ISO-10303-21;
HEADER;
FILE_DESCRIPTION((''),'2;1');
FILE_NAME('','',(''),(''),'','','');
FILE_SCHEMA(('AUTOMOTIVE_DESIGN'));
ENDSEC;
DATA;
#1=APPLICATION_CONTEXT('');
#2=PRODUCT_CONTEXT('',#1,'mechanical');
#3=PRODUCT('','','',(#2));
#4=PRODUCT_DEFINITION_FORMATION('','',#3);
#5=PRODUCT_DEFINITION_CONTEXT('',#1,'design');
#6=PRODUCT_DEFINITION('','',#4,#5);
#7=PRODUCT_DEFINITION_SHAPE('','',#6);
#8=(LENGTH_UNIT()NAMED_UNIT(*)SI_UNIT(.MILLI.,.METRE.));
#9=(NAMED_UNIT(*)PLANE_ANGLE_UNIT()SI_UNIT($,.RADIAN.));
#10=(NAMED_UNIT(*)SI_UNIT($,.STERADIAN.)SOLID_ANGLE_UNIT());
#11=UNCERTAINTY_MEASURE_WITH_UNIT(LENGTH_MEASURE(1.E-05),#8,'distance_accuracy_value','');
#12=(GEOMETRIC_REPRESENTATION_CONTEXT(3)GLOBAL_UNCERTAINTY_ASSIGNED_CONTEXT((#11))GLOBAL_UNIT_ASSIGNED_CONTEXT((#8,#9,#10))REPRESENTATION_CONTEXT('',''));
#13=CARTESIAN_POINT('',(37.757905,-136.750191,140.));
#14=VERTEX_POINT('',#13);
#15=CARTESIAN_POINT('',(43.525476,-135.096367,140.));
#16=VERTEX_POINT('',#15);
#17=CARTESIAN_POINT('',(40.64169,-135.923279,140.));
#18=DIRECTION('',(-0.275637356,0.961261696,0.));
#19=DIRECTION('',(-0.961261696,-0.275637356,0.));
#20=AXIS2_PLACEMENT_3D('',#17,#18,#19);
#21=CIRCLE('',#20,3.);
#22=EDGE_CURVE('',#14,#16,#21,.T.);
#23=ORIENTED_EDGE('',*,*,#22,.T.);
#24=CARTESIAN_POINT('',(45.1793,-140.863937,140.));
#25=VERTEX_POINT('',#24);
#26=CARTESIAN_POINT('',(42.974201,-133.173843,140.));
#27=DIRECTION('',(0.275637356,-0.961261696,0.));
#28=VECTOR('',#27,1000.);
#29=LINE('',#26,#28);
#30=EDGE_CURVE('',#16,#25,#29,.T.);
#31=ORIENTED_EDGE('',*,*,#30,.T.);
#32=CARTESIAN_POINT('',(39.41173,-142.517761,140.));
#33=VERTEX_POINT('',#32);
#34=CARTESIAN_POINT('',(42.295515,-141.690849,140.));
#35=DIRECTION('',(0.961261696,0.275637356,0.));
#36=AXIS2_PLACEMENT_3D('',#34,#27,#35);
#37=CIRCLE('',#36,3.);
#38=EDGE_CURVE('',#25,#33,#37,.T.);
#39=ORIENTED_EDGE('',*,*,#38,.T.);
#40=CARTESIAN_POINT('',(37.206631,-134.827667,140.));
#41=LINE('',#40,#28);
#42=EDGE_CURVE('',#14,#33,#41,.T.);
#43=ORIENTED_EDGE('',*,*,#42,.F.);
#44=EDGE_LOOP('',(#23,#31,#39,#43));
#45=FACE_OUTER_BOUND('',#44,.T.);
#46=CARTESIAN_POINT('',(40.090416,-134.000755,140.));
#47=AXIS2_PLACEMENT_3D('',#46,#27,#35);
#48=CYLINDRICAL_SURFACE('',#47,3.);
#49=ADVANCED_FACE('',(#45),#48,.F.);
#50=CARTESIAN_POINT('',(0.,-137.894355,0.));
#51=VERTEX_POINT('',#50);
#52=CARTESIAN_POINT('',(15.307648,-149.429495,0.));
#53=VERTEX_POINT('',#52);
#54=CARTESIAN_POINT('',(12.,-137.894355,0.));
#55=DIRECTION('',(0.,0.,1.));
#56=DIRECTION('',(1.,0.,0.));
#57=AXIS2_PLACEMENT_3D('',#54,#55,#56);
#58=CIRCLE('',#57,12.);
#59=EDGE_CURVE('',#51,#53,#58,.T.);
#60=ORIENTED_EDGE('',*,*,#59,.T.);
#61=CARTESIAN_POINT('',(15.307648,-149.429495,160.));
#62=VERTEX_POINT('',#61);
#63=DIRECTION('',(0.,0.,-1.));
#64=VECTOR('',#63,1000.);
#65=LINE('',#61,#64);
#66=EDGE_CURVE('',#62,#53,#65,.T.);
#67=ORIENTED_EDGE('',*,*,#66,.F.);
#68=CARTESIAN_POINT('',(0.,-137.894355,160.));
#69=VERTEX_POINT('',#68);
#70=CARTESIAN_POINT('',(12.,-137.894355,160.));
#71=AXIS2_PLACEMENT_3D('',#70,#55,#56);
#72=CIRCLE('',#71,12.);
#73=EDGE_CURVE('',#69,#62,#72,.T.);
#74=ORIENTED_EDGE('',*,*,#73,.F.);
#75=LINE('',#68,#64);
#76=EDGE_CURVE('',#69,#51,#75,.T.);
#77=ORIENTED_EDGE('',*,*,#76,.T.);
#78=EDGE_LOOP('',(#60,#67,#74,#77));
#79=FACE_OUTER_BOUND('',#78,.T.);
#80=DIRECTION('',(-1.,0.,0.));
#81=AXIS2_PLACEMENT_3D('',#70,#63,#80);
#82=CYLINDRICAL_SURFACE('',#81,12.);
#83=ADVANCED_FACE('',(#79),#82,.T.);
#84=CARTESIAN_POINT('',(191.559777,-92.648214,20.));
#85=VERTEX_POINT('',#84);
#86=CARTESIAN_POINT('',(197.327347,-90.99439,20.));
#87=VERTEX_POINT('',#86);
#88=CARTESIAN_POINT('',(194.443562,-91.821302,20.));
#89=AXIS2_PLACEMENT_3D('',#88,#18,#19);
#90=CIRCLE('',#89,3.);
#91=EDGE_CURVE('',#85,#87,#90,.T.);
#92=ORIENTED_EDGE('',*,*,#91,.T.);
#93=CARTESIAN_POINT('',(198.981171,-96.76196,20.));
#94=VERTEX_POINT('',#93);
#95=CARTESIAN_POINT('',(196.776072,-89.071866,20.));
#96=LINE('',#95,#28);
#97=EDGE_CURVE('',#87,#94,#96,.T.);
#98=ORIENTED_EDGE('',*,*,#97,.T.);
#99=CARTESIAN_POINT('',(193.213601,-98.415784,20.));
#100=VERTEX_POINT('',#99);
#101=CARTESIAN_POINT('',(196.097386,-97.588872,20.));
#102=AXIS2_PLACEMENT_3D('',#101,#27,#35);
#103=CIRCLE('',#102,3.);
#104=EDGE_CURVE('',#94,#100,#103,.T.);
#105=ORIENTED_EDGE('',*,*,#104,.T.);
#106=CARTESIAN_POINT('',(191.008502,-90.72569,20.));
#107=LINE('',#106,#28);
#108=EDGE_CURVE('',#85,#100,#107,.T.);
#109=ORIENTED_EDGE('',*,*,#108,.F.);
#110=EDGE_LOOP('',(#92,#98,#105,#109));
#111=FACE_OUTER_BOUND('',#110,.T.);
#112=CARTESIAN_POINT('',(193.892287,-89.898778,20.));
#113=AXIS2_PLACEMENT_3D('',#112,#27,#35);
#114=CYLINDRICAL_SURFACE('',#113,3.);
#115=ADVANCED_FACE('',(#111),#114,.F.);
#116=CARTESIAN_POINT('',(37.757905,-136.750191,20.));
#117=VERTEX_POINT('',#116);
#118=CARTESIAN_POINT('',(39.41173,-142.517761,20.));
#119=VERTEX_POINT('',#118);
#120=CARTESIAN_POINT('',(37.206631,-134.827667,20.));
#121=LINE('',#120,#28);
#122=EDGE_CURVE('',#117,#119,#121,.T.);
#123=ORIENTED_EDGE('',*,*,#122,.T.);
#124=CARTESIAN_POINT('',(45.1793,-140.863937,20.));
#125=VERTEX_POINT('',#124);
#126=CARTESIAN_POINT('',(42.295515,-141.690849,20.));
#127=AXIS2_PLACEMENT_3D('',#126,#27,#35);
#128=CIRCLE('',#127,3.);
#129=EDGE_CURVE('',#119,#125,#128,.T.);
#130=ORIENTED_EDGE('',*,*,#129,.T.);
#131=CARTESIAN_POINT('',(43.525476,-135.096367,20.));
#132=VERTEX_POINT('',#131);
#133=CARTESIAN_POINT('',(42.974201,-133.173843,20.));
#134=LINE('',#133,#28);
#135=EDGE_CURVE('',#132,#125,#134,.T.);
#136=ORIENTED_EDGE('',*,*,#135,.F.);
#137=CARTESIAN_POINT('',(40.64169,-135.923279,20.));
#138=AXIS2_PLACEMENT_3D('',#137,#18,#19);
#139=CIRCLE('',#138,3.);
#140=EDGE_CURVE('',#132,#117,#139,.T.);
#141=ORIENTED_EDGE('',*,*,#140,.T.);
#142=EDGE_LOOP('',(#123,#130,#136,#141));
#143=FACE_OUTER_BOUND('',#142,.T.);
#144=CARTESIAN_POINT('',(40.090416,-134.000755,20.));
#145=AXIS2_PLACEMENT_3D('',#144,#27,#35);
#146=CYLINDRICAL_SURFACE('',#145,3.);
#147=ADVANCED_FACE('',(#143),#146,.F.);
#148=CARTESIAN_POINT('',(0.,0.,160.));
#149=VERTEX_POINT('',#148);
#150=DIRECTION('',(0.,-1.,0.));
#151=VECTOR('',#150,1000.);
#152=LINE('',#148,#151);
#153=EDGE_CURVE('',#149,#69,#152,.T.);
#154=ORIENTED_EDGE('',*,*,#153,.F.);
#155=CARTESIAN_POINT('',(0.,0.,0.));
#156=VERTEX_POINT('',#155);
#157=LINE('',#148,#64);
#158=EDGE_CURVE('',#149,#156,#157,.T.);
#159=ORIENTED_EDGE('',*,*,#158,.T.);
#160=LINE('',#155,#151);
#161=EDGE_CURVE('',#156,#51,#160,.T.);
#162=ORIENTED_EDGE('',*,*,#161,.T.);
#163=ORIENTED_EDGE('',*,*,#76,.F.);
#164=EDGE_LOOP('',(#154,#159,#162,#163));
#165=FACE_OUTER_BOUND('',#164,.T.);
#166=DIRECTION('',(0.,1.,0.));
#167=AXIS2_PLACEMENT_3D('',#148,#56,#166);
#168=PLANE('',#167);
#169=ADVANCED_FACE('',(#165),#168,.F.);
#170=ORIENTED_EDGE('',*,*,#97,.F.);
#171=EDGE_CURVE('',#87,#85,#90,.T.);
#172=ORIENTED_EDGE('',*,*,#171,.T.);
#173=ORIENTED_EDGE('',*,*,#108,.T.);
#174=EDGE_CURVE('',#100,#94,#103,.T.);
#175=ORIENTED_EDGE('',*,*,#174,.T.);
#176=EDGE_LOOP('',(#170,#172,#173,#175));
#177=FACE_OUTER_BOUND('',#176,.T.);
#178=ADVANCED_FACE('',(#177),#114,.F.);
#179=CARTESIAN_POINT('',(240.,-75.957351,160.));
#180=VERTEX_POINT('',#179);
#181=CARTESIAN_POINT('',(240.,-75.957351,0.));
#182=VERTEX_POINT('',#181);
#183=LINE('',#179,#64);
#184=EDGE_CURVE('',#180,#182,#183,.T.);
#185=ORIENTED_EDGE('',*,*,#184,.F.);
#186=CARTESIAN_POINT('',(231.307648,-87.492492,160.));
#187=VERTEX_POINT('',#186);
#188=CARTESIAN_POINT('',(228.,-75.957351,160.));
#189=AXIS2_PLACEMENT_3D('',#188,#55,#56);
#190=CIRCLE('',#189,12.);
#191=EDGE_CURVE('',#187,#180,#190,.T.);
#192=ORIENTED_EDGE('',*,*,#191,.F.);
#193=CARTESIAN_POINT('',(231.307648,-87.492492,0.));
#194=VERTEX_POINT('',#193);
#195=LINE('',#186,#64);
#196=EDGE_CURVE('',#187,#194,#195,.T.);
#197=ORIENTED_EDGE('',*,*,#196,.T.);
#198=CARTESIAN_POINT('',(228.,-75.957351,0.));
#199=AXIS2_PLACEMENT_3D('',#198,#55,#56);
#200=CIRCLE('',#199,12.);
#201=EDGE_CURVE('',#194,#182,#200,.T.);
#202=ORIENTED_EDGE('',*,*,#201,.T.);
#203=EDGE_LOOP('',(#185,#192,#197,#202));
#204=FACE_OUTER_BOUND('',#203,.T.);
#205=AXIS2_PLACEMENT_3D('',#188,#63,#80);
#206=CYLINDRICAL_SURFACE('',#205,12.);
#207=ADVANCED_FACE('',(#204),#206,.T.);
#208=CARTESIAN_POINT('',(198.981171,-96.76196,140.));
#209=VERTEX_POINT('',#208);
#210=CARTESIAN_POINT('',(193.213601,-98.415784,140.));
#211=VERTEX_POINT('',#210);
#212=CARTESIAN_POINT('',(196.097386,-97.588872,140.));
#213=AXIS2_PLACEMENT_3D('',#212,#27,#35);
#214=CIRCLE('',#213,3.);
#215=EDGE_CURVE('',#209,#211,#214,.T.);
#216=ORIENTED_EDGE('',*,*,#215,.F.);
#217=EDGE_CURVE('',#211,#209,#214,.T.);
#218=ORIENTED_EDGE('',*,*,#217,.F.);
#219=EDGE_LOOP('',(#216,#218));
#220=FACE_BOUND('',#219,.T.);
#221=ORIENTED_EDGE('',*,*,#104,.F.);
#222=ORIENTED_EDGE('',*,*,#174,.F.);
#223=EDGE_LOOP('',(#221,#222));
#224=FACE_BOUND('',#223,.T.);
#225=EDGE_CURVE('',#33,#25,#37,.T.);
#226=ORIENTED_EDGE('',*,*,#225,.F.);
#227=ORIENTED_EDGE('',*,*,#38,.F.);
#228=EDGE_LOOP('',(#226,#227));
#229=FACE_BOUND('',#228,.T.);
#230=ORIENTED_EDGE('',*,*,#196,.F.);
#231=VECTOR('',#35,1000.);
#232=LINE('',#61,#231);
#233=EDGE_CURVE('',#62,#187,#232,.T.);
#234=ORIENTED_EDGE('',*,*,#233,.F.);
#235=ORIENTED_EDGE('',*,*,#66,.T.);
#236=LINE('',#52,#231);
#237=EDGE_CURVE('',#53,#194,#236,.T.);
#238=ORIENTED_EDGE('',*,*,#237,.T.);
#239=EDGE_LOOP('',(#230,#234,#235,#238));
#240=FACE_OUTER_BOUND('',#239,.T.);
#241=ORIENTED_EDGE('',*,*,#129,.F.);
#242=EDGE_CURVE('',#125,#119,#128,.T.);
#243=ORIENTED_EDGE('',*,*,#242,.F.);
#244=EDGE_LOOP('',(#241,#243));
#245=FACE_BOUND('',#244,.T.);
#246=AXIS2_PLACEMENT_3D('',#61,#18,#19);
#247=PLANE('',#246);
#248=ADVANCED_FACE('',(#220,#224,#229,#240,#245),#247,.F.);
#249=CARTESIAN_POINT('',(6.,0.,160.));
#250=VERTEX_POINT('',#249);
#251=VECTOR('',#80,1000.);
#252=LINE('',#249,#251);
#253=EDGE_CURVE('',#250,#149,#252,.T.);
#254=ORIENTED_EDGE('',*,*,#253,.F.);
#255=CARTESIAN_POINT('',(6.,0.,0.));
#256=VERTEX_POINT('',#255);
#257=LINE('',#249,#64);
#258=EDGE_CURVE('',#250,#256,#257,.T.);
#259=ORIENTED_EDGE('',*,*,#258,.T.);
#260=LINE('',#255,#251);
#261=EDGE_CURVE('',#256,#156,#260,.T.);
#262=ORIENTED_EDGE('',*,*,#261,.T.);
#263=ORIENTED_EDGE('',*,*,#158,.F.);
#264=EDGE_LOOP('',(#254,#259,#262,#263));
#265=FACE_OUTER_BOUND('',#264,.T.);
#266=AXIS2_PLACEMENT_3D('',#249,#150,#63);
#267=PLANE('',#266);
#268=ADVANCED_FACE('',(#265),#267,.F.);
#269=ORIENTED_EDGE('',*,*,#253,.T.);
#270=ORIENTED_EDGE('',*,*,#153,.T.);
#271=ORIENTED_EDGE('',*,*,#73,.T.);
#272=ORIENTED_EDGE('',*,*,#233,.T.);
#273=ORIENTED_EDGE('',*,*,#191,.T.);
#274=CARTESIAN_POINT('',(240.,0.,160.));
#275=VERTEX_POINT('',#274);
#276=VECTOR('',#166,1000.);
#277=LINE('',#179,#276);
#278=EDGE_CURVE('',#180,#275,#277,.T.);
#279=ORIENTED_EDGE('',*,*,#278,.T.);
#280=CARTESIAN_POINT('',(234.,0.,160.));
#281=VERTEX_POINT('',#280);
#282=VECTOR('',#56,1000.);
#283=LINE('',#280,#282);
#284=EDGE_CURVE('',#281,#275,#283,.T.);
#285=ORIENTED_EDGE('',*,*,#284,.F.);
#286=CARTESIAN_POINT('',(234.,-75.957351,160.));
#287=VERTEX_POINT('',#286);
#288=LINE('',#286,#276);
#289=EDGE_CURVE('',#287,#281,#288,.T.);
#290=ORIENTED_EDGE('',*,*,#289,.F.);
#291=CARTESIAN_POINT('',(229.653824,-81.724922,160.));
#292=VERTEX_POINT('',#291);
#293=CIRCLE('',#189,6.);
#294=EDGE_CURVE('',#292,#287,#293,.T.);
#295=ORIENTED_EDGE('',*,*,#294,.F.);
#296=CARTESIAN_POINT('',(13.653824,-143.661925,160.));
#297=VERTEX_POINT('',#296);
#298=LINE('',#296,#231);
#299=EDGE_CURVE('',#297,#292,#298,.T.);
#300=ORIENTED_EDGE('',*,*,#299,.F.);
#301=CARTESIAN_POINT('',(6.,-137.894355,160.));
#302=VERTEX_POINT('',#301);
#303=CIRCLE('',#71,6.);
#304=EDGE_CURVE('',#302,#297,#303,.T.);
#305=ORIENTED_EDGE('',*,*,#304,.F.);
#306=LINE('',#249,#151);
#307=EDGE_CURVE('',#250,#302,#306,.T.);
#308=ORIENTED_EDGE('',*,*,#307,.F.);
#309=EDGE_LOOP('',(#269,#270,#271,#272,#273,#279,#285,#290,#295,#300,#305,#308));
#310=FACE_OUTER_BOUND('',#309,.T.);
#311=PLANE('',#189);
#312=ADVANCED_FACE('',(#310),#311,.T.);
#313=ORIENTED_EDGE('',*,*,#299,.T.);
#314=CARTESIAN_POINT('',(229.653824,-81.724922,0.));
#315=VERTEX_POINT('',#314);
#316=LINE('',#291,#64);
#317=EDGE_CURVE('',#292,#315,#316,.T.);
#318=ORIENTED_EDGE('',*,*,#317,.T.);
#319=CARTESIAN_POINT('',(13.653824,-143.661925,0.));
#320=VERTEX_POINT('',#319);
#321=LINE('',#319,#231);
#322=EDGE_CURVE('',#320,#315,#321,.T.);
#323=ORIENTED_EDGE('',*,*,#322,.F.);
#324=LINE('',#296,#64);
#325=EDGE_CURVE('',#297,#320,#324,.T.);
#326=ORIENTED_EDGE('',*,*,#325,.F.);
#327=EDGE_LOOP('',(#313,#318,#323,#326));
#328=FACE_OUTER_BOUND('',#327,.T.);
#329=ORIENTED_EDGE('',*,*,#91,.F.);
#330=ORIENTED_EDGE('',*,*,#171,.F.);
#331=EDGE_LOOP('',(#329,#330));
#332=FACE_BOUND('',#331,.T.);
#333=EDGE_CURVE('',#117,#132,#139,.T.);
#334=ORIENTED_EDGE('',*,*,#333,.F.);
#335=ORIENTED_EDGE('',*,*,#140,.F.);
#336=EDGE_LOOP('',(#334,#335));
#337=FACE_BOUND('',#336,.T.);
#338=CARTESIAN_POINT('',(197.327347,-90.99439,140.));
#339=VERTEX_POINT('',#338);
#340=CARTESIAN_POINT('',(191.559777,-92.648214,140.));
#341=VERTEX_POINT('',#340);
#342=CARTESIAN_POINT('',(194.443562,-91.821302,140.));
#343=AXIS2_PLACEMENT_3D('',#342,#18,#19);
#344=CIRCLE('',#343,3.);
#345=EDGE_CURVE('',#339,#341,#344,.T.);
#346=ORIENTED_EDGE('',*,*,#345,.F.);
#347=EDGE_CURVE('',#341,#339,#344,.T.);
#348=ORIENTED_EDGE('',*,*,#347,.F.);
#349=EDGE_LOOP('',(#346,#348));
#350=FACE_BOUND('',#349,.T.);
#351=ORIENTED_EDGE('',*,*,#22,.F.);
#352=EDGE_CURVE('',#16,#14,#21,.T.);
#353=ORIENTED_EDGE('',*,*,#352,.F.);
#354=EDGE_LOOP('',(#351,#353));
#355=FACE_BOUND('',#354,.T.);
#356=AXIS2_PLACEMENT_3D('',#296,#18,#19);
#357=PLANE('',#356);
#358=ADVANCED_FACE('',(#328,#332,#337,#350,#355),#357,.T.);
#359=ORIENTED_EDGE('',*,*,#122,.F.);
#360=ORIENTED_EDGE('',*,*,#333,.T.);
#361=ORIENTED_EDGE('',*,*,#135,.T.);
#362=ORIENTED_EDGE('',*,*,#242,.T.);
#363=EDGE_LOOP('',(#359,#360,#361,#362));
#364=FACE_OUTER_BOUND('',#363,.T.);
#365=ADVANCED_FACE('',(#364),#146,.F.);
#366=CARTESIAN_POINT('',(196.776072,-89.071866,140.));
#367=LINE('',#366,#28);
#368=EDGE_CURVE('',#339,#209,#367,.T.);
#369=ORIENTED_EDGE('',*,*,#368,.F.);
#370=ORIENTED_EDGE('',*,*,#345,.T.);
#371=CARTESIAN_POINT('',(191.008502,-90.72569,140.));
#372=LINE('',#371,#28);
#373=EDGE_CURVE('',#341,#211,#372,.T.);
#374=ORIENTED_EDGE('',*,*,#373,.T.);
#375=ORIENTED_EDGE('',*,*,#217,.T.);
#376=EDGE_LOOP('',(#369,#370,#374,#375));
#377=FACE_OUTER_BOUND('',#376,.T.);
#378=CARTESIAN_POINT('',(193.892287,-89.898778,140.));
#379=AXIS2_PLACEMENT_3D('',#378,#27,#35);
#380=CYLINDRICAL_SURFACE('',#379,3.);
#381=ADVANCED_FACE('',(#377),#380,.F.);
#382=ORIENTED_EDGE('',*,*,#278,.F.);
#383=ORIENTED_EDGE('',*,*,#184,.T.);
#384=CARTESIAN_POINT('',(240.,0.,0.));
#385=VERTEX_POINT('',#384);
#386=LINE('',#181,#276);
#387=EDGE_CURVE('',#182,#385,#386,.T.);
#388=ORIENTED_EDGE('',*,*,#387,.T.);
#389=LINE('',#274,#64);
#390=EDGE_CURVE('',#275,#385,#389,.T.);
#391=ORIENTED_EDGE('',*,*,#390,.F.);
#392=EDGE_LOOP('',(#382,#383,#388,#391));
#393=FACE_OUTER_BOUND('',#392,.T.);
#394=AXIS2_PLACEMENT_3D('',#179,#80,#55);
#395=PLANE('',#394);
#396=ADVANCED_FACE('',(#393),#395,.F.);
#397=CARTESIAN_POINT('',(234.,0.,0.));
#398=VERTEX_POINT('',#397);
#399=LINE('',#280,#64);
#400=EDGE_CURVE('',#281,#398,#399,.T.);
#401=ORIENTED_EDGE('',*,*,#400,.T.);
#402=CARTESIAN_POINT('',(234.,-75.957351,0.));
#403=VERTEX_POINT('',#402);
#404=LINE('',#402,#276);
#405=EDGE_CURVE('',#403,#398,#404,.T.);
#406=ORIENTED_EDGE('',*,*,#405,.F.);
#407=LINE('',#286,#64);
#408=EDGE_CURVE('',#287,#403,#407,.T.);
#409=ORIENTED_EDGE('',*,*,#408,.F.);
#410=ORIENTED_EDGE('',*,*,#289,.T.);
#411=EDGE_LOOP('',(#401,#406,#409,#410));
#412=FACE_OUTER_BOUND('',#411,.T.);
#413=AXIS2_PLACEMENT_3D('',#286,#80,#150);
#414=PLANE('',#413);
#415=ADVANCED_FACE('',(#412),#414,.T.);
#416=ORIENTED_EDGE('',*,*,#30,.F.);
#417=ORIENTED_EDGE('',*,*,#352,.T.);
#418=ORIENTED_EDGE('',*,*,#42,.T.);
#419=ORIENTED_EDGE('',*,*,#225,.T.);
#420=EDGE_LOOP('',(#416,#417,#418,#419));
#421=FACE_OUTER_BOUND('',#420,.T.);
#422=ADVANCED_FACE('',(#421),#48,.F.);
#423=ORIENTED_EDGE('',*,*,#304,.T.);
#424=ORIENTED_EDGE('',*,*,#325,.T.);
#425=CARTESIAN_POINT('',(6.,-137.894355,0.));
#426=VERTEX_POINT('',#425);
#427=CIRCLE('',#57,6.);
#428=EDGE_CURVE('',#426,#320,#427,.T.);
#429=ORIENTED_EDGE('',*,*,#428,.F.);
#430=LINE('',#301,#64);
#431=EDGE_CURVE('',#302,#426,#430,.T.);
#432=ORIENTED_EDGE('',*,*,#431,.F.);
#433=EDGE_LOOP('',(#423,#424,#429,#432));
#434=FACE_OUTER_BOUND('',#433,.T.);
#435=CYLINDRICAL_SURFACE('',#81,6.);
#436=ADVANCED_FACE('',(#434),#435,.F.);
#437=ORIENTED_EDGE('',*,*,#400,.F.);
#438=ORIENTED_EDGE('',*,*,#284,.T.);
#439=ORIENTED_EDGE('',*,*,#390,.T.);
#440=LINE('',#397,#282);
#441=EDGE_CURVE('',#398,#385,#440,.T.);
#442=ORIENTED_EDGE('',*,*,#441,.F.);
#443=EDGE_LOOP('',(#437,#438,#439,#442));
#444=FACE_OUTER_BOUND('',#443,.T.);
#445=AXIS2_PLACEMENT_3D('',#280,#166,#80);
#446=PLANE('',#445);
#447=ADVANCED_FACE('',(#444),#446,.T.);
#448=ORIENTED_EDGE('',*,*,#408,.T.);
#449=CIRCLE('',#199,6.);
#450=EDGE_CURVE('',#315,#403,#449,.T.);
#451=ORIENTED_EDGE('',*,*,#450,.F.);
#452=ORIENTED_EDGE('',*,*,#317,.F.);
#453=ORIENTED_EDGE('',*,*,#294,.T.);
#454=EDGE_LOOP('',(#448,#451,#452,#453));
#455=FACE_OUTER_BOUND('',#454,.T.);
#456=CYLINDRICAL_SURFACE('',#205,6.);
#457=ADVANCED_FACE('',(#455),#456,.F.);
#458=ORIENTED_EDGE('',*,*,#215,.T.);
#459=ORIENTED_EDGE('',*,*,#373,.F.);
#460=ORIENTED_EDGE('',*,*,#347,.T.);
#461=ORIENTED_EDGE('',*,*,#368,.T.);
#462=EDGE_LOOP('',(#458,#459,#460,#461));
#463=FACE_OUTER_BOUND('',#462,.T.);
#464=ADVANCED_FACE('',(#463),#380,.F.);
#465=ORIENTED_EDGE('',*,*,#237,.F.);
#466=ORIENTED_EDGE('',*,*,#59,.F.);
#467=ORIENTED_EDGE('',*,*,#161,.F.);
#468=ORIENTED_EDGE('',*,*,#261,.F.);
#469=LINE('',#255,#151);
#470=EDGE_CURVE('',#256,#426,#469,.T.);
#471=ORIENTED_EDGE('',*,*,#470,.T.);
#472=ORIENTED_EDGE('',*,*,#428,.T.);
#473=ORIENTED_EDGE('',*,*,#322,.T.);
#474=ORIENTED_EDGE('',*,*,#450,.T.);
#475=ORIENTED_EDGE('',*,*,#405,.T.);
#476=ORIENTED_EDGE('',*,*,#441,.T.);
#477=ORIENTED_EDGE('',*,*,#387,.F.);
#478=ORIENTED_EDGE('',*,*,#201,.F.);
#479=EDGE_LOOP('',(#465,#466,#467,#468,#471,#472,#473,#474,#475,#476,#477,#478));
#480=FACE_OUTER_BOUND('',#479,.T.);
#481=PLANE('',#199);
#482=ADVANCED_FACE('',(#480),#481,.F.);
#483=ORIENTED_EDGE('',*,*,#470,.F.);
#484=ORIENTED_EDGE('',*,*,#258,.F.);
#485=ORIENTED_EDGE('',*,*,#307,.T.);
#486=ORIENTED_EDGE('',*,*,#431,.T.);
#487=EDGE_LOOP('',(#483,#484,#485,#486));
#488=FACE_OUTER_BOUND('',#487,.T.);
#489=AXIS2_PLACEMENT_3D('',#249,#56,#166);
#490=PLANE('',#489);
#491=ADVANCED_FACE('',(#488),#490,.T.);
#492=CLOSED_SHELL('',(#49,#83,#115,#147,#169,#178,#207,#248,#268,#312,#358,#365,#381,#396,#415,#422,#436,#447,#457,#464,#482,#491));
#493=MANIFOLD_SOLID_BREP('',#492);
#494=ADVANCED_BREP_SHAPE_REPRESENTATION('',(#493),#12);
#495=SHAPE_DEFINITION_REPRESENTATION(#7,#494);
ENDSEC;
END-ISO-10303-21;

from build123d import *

# Parameters (mm, degrees)
BOSS_EXTRUDE1_DEPTH = 160
SKETCH2_R           = 3
CUT_EXTRUDE1_DEPTH  = 8


with BuildPart() as part:
    # Sketch1 → Boss-Extrude1 (new body)
    with BuildSketch(Plane.XY):
        with BuildLine():
            Line((0, 0), (0, -137.894354723))
            ThreePointArc((0, -137.894354723), (4.778219722, -147.477980843), (15.30764827, -149.429495074))
            Line((15.30764827, -149.429495074), (231.30764827, -87.49249175))
            ThreePointArc((231.30764827, -87.49249175), (237.583626121, -83.179131677), (240, -75.957351399))
            Line((240, -75.957351399), (240, 0))
            Line((240, 0), (234, 0))
            Line((234, 0), (234, -75.957351399))
            ThreePointArc((234, -75.957351399), (232.79181306, -79.568241538), (229.653824135, -81.724921574))
            Line((229.653824135, -81.724921574), (13.653824135, -143.661924898))
            ThreePointArc((13.653824135, -143.661924898), (8.389109861, -142.686167783), (6, -137.894354723))
            Line((6, -137.894354723), (6, 0))
            Line((6, 0), (0, 0))
        make_face()
    extrude(amount=BOSS_EXTRUDE1_DEPTH)

    # Sketch2 → Cut-Extrude1 (cut)
    with BuildSketch(Plane(origin=(40.755797191, -142.132355795, 0), x_dir=(0.9612616959383188, 0.2756373558169997, 0), z_dir=(0.27563735581699966, -0.9612616959383187, 0))):
        with Locations((1.601767174, 140)):
            Circle(SKETCH2_R)
        with Locations((1.601767174, 20)):
            Circle(SKETCH2_R)
        with Locations((161.601767174, 140)):
            Circle(SKETCH2_R)
        with Locations((161.601767174, 20)):
            Circle(SKETCH2_R)
    extrude(amount=-CUT_EXTRUDE1_DEPTH, mode=Mode.SUBTRACT)


solid = part.part
